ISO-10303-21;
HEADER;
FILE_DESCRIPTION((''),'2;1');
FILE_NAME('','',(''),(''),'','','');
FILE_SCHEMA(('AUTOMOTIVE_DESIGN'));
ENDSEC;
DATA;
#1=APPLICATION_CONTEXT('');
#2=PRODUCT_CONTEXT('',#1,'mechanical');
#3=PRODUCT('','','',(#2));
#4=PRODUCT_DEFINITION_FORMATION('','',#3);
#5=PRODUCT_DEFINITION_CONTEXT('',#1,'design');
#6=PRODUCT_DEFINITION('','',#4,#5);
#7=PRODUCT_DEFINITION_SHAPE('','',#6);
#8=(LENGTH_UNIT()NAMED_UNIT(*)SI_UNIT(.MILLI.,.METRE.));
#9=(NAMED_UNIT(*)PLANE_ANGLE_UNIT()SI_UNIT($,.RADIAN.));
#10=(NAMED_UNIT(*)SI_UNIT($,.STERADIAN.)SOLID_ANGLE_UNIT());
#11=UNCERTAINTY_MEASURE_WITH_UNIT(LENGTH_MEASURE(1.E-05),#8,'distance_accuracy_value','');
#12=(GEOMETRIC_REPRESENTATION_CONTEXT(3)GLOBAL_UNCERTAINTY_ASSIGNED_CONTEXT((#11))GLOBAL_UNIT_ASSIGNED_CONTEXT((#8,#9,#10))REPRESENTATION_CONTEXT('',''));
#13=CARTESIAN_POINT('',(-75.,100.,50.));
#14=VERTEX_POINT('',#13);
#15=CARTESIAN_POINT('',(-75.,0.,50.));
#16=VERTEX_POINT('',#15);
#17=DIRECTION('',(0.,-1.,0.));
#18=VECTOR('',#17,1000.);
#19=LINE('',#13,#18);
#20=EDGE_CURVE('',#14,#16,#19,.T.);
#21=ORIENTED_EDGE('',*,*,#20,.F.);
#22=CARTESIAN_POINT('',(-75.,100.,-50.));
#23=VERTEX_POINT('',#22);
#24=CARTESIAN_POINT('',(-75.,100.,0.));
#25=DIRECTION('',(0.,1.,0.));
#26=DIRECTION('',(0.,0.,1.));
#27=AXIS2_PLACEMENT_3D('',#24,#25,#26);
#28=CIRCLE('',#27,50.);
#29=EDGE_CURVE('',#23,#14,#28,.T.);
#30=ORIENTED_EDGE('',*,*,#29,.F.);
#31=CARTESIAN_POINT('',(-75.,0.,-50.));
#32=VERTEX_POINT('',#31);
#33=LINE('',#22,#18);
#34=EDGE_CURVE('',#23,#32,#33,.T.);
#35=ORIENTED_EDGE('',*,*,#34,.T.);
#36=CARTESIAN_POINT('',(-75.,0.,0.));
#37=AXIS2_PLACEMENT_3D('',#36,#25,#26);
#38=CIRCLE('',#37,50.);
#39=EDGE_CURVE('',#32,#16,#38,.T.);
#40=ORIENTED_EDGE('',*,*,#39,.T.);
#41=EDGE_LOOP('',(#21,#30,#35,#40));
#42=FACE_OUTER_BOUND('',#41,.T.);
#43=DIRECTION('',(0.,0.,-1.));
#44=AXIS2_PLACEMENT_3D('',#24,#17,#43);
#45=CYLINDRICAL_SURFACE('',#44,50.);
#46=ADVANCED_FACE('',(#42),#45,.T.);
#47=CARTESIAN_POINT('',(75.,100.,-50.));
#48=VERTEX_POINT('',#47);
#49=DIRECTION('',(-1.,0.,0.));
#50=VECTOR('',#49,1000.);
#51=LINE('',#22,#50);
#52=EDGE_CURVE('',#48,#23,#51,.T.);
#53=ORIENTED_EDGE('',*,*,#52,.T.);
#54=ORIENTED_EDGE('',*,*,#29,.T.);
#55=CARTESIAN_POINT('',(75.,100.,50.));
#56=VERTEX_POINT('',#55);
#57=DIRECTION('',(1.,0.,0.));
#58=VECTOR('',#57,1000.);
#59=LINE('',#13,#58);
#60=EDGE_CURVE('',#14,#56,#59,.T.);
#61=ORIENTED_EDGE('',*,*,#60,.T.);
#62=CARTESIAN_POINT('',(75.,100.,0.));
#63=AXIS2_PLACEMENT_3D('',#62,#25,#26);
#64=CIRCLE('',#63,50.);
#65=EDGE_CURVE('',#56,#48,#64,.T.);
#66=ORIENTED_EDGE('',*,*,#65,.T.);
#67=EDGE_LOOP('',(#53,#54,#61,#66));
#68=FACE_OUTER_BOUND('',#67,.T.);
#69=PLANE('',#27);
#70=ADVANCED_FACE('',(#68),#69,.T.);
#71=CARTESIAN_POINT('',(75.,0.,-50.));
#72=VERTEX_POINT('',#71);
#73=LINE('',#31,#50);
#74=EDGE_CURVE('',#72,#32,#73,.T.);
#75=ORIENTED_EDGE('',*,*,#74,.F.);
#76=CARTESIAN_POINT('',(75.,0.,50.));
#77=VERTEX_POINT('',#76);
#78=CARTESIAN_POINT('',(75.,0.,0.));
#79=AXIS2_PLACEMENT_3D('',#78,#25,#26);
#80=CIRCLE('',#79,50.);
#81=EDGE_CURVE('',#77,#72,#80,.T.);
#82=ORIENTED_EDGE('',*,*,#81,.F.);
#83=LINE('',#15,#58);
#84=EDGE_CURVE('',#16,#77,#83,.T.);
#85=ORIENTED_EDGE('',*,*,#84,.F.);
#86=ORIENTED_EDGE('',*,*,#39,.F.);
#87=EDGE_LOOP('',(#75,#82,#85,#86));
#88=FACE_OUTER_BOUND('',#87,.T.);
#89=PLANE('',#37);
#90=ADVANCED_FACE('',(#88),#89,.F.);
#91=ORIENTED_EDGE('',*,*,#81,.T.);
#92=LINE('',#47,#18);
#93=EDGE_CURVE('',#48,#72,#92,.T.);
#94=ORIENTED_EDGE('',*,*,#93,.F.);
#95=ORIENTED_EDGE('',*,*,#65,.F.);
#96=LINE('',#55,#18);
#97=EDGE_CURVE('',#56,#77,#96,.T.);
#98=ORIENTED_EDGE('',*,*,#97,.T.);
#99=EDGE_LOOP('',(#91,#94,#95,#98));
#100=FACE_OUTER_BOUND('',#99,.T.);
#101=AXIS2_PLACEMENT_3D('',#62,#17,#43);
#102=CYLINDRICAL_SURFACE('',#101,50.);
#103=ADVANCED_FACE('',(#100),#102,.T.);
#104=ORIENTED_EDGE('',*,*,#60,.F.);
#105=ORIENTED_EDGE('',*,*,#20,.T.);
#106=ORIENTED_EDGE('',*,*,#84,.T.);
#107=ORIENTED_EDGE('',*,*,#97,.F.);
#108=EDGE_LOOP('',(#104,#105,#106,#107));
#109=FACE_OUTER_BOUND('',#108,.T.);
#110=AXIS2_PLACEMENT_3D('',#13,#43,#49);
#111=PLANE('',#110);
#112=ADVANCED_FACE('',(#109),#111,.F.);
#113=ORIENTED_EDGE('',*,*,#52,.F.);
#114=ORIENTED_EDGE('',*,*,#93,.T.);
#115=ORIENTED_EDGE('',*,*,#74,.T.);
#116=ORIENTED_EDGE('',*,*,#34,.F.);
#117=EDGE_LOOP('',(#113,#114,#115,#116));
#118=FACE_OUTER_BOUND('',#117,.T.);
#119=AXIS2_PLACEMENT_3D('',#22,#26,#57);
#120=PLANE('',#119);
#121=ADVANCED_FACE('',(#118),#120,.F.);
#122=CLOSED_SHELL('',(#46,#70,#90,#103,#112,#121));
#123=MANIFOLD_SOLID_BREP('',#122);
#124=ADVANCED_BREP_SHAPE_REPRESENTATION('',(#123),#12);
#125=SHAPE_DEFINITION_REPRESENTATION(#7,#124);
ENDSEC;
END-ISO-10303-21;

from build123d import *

# Parameters (mm, degrees)
BOSS_EXTRUDE1_DEPTH = 100


with BuildPart() as part:
    # Sketch1 → Boss-Extrude1 (new body)
    with BuildSketch(Plane(origin=(0, 0, 0), x_dir=(1, 0, 0), z_dir=(0, 1, 0))):
        with BuildLine():
            Line((-75, 50), (75, 50))
            ThreePointArc((75, 50), (125, 0), (75, -50))
            Line((75, -50), (-75, -50))
            ThreePointArc((-75, -50), (-125, 0), (-75, 50))
        make_face()
    extrude(amount=BOSS_EXTRUDE1_DEPTH)


solid = part.part
